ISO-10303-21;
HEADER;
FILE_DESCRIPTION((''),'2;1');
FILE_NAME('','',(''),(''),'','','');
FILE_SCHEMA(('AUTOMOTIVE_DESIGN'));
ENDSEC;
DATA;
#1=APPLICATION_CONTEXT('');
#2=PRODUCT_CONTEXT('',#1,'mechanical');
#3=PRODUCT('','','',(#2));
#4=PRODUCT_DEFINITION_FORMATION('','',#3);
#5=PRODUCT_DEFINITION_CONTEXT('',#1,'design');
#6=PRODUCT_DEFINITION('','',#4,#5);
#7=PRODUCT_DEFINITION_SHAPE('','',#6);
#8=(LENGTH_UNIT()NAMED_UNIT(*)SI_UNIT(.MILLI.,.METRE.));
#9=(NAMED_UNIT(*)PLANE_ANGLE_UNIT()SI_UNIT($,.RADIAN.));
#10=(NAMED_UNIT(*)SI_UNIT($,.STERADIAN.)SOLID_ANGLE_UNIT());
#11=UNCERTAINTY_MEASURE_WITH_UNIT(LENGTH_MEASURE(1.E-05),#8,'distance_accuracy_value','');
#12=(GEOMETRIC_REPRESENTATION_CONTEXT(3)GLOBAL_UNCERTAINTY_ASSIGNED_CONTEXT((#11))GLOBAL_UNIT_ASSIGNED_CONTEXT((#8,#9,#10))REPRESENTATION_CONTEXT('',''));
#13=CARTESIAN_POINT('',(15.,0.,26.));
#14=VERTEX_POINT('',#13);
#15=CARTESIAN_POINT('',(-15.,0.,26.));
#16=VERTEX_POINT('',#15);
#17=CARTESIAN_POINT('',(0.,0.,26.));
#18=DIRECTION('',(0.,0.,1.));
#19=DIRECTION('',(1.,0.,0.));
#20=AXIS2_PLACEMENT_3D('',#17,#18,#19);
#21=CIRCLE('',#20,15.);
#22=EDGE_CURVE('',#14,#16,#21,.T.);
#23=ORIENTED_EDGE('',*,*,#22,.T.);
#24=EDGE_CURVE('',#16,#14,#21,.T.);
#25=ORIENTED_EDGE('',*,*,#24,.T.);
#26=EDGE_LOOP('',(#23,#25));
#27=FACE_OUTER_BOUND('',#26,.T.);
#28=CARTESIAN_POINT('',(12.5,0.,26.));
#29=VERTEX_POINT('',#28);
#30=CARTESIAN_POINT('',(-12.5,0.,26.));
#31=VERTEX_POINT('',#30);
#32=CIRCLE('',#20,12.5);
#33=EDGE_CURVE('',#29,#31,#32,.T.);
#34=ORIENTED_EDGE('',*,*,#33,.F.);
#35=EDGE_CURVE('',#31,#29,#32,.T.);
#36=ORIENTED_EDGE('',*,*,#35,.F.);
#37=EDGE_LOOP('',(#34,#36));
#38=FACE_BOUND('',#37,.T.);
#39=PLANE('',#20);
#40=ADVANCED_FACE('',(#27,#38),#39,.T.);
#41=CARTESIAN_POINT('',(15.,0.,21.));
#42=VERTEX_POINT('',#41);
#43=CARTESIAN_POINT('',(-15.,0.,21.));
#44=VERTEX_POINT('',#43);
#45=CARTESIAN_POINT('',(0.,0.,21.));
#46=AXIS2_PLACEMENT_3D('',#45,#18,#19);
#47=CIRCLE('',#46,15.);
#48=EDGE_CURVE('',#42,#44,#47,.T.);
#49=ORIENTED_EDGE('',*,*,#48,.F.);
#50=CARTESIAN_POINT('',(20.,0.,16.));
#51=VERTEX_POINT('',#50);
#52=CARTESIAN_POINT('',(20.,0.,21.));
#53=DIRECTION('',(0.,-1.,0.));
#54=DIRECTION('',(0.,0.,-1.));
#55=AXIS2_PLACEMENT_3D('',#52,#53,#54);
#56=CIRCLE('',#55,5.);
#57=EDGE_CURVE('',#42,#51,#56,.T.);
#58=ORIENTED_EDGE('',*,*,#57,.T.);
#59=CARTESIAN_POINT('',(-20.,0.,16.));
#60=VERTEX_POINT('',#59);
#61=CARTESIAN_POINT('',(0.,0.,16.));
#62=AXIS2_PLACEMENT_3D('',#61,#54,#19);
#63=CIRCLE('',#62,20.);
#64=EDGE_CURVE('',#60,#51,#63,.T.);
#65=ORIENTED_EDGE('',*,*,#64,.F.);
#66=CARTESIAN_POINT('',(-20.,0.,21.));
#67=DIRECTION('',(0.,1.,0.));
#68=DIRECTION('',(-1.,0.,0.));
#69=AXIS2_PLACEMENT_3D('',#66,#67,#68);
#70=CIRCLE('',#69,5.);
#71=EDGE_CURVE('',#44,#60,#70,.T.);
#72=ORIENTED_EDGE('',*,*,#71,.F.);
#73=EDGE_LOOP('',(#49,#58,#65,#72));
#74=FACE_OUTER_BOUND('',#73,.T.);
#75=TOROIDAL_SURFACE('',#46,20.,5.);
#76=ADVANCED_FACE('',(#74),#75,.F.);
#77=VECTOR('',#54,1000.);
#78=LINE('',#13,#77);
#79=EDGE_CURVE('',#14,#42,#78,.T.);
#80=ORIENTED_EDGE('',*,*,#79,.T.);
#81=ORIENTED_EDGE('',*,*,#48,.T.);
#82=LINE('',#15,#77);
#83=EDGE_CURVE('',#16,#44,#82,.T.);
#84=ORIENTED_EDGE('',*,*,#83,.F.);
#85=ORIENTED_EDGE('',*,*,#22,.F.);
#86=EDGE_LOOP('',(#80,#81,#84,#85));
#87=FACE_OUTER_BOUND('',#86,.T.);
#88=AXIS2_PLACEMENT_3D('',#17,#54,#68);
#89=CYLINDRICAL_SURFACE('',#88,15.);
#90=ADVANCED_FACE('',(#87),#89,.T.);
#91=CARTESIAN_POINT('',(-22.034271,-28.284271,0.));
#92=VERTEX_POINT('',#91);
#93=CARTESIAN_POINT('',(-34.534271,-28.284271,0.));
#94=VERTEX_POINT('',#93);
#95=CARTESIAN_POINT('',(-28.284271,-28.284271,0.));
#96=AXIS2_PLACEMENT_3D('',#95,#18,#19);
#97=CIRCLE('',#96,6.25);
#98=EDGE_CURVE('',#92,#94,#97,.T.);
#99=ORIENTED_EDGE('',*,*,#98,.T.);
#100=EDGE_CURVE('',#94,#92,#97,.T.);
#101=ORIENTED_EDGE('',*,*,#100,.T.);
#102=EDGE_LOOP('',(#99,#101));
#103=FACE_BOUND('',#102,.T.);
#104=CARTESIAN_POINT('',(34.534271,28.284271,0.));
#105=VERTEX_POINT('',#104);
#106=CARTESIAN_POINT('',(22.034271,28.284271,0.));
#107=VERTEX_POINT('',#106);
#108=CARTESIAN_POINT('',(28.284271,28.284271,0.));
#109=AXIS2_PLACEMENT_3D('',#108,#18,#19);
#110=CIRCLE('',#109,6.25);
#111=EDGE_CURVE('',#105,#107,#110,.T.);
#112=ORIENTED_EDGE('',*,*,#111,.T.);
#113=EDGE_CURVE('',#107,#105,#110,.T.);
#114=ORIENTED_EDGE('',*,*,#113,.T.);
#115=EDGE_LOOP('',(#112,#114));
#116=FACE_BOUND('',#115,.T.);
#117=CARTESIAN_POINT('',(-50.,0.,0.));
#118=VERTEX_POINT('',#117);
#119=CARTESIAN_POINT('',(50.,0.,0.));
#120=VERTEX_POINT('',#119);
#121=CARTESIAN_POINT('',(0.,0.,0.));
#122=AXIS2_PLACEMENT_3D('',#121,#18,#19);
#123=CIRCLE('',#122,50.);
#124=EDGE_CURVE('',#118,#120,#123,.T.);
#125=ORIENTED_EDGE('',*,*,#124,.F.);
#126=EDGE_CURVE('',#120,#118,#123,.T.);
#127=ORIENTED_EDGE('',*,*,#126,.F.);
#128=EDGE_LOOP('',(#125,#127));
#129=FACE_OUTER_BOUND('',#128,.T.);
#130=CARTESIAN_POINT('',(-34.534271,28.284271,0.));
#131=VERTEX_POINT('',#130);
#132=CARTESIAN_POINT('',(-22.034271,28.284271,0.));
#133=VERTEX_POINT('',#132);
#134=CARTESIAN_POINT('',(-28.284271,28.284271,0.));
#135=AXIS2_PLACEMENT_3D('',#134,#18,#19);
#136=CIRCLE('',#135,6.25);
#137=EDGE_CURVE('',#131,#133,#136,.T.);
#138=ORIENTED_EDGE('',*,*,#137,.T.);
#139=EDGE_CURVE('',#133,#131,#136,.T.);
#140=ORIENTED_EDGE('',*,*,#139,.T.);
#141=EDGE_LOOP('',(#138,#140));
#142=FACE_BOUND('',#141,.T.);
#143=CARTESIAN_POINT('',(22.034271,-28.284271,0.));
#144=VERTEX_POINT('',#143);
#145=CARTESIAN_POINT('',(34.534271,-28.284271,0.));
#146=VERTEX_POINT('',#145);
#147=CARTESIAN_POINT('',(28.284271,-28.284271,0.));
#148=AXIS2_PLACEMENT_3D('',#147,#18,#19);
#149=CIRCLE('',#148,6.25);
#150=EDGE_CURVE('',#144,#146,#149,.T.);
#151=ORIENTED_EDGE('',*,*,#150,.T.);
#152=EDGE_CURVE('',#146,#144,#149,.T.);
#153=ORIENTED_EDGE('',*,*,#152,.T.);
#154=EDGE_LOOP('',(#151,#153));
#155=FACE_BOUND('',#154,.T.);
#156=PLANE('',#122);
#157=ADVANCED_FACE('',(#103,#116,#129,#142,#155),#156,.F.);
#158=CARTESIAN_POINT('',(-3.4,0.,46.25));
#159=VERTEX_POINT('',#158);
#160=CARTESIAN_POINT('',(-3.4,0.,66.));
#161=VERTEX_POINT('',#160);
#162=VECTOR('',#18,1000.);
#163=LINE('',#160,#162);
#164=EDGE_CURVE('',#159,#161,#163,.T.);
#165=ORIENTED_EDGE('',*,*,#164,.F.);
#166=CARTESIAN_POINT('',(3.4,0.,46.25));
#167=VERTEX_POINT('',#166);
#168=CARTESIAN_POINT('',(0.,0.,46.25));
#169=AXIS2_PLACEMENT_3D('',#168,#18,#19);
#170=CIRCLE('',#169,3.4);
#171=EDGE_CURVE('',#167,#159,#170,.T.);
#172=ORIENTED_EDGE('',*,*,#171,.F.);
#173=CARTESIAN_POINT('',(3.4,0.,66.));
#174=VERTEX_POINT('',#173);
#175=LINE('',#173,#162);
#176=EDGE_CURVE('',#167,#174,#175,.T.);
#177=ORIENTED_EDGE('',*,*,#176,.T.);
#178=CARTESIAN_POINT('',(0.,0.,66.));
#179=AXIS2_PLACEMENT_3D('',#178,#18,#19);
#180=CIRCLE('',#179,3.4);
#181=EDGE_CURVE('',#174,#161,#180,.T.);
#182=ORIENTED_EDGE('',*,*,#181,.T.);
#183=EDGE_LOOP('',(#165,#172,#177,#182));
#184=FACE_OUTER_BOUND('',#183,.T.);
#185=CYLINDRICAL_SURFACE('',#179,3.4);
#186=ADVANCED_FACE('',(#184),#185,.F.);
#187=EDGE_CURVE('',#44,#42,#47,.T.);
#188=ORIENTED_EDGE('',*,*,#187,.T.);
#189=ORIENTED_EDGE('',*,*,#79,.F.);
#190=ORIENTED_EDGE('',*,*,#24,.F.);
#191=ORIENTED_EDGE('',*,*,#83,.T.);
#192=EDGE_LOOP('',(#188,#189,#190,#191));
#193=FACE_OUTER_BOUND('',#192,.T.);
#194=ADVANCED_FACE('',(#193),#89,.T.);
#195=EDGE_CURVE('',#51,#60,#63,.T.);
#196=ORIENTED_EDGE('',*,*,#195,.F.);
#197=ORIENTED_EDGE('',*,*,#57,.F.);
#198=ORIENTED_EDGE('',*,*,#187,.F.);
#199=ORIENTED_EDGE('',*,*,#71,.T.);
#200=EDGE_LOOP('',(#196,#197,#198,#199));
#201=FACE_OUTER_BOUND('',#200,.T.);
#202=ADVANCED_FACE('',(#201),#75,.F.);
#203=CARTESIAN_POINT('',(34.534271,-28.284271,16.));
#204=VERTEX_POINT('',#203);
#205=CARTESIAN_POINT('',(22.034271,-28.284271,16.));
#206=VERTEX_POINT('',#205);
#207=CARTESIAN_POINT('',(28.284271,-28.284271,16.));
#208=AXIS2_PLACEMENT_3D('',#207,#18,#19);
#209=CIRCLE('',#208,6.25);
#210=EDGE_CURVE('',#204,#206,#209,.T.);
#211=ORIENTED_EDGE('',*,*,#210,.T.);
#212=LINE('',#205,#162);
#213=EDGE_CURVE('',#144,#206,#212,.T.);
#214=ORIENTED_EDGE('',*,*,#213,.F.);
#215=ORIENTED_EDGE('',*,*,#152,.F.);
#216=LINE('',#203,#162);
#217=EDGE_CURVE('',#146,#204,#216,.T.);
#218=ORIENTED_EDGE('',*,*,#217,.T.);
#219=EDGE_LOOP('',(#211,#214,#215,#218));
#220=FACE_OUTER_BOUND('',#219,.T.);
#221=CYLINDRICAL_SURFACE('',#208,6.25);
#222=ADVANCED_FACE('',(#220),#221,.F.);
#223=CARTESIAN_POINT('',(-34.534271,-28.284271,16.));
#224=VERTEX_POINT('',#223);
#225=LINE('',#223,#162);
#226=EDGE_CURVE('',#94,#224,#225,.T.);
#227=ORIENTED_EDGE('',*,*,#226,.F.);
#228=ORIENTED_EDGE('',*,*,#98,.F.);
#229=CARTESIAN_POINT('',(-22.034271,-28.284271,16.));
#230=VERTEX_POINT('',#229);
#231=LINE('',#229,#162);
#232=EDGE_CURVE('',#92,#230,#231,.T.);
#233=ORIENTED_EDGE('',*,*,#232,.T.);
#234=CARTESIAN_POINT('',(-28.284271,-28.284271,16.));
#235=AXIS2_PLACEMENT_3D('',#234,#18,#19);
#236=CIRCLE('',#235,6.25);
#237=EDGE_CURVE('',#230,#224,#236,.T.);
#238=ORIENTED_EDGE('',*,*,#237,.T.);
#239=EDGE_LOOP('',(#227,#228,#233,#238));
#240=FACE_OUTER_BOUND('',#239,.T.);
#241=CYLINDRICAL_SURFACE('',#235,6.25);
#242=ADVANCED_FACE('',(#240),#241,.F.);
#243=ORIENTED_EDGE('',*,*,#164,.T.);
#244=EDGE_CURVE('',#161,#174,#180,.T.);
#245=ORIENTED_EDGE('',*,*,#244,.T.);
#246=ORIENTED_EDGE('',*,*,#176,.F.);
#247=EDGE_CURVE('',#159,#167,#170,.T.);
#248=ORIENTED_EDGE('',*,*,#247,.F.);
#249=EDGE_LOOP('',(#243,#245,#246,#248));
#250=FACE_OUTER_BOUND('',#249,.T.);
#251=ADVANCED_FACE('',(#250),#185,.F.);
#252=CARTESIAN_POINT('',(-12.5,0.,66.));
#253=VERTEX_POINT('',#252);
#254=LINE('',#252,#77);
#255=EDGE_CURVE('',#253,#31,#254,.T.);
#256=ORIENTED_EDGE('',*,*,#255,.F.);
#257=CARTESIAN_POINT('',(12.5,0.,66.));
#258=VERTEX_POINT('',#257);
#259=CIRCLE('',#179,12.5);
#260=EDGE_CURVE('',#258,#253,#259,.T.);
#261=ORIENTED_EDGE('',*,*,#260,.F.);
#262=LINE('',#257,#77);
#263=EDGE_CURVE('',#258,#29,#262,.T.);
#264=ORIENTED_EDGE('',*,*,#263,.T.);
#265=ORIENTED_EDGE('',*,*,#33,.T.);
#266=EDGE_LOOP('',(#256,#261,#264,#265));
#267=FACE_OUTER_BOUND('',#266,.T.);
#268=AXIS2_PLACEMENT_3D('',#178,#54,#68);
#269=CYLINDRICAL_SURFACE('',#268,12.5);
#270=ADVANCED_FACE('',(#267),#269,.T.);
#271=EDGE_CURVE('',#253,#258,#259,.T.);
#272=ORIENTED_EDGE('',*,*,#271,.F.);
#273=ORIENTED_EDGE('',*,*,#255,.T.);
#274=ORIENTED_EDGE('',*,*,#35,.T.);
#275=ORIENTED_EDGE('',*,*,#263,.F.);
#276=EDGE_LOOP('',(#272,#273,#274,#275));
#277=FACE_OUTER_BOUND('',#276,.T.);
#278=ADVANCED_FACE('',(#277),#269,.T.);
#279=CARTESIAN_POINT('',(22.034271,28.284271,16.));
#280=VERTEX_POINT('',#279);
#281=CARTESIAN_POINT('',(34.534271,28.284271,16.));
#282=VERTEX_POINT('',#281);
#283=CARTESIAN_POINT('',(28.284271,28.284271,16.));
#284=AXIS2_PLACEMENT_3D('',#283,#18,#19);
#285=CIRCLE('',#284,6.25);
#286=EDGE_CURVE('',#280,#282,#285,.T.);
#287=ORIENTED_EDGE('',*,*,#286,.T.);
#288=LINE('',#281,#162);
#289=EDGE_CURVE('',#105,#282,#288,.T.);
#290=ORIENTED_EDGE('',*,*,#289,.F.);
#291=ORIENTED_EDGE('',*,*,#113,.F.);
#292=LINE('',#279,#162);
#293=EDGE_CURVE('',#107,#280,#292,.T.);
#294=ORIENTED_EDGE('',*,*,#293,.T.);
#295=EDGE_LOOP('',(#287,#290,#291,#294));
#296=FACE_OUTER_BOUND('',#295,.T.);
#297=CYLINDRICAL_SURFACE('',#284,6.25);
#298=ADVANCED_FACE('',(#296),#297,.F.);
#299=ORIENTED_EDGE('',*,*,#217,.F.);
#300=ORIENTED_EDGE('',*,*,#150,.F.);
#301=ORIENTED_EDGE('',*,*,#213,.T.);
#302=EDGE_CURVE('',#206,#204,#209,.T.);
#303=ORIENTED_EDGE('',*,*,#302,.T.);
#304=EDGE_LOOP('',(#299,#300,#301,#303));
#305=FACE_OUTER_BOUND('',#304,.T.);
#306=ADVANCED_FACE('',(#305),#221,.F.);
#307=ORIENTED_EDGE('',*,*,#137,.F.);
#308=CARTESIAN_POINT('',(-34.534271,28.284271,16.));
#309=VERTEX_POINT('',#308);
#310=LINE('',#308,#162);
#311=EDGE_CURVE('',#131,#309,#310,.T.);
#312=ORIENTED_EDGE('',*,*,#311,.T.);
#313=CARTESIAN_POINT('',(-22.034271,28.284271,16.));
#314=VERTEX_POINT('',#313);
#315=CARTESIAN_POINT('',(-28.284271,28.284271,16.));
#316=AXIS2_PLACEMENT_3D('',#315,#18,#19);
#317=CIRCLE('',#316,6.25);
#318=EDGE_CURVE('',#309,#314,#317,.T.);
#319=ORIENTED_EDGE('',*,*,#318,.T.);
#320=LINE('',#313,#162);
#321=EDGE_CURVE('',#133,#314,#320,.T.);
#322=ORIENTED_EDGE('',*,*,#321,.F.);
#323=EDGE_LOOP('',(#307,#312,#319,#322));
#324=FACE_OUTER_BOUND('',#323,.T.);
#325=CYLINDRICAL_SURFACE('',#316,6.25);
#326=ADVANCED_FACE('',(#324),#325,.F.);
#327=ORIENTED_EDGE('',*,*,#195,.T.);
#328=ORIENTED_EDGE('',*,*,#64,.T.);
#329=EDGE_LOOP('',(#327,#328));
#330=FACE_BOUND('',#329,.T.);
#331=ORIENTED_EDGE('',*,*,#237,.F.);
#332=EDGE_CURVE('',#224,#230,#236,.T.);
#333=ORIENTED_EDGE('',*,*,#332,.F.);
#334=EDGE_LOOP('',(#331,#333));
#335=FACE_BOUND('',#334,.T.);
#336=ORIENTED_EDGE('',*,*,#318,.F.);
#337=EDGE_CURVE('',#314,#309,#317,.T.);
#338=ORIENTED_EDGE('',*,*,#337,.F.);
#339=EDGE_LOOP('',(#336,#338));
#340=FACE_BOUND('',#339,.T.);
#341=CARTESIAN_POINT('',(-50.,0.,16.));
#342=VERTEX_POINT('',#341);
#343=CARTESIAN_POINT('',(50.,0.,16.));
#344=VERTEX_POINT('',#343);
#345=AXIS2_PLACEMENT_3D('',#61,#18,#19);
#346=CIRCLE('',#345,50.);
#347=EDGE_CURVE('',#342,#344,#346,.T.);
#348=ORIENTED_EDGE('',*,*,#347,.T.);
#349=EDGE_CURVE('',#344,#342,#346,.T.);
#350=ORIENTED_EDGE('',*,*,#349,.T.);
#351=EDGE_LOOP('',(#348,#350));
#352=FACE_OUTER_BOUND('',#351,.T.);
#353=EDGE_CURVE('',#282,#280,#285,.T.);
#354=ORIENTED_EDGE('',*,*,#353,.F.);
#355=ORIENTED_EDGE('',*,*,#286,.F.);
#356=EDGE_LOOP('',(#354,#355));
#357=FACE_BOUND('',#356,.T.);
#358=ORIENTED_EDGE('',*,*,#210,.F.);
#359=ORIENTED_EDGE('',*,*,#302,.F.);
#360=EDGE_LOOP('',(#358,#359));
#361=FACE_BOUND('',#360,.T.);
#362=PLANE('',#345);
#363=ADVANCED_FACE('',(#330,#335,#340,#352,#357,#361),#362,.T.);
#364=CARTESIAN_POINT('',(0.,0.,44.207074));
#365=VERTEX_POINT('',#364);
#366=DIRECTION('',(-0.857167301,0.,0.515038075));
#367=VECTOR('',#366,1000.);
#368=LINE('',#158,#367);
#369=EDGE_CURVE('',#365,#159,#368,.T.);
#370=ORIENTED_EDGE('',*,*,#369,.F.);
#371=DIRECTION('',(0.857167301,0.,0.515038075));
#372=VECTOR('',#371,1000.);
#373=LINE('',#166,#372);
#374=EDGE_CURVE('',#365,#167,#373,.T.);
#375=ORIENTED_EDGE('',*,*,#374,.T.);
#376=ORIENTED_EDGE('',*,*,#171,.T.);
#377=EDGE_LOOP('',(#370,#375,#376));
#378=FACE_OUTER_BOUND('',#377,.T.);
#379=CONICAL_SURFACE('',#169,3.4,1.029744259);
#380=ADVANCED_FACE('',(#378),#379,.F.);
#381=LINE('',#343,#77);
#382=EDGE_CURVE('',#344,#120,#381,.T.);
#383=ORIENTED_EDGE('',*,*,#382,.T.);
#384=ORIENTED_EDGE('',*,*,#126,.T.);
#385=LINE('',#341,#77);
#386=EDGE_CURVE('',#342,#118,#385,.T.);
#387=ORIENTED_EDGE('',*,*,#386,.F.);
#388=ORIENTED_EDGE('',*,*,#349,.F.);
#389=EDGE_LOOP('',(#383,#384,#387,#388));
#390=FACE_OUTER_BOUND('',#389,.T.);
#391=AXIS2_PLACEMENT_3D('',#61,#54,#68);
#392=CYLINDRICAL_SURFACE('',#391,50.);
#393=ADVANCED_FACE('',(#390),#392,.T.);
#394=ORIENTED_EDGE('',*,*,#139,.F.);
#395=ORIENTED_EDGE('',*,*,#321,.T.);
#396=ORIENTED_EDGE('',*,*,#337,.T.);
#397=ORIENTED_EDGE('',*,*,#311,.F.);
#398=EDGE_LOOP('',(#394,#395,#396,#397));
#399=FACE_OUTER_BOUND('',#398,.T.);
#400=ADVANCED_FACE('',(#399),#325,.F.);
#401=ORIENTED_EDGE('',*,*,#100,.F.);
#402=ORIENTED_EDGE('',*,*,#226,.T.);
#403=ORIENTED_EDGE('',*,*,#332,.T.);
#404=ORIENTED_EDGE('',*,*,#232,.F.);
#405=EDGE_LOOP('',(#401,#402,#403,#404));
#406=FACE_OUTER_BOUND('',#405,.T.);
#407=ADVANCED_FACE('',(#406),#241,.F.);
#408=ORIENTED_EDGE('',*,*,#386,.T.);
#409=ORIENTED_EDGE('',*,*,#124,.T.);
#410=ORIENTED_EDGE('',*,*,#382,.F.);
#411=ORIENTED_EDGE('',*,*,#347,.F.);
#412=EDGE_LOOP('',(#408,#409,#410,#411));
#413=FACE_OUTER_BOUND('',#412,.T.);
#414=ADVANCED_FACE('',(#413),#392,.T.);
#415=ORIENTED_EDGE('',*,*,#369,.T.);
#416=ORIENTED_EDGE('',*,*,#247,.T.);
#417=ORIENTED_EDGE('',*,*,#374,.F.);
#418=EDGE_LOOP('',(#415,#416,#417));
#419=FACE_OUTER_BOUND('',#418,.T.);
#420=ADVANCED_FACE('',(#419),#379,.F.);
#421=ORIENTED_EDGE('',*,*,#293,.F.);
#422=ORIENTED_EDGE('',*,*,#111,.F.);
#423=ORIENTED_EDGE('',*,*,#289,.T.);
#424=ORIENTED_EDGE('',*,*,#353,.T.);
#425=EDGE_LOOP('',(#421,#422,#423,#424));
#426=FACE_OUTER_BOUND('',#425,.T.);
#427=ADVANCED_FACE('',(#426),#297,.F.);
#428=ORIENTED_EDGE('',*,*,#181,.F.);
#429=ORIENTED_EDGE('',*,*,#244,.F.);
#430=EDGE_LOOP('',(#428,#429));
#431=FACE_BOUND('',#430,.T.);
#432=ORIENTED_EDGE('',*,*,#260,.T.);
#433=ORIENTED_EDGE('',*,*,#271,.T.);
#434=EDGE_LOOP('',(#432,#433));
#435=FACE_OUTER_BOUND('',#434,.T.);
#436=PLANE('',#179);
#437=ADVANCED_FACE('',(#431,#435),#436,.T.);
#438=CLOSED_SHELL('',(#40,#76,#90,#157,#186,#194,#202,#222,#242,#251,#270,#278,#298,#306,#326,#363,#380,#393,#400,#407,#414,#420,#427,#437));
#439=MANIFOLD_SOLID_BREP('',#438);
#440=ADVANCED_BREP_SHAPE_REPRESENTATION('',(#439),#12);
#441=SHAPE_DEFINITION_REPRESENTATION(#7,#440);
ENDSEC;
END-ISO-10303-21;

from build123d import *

# Parameters (mm, degrees)
SKETCH_1_R                = 50
EXTRUDE_1_DEPTH           = 16
SKETCH_2_R                = 15
EXTRUDE_2_DEPTH           = 10
SKETCH_3_R                = 12.5
EXTRUDE_3_DEPTH           = 40
HOLE_WIZARD_12_5_12_5_1_D = 12.5
PATTERN_CIRCULAR_1_COUNT  = 4
HOLE_WIZARD_M8_1_D        = 6.8
HOLE_WIZARD_M8_1_DEPTH    = 19.75
HOLE_WIZARD_M8_1_TIP      = 2.042926105
FILLET_1_R                = 5


with BuildPart() as part:
    # 草图1 → 凸台-拉伸1 (new body)
    with BuildSketch(Plane.XY):
        Circle(SKETCH_1_R)
    extrude(amount=EXTRUDE_1_DEPTH)

    # 草图2 → 凸台-拉伸2 (add)
    with BuildSketch(Plane.XY.offset(16)):
        Circle(SKETCH_2_R)
    extrude(amount=EXTRUDE_2_DEPTH)

    # 草图3 → 凸台-拉伸3 (add)
    with BuildSketch(Plane.XY.offset(26)):
        Circle(SKETCH_3_R)
    extrude(amount=EXTRUDE_3_DEPTH)

    # Ø12.5 (12.5) 直径孔1 (through all)
    with Locations(Plane.XY.offset(16)):
        with Locations((-28.284271247, 28.284271247)):
            hole_wizard_12_5_12_5_1 = Hole(HOLE_WIZARD_12_5_12_5_1_D / 2)

    # 阵列(圆周)1: Ø12.5 (12.5) 直径孔1 ×4 about axis
    pattern_circular_1_axis = Axis((0, 0, 0), (0, 0, 1))
    for i in range(1, PATTERN_CIRCULAR_1_COUNT):
        add(hole_wizard_12_5_12_5_1.rotate(pattern_circular_1_axis, i * 360 / PATTERN_CIRCULAR_1_COUNT), mode=Mode.SUBTRACT)

    # M8 螺纹孔1
    with Locations(Plane.XY.offset(66)):
        with Locations((0, 0)):
            Hole(HOLE_WIZARD_M8_1_D / 2, depth=HOLE_WIZARD_M8_1_DEPTH)
            with Locations((0, 0, -(HOLE_WIZARD_M8_1_DEPTH + HOLE_WIZARD_M8_1_TIP / 2))):  # 118° drill point
                Cone(0, HOLE_WIZARD_M8_1_D / 2, HOLE_WIZARD_M8_1_TIP, mode=Mode.SUBTRACT)

    # 圆角1
    fillet_1_edges = [part.edges().sort_by_distance(p)[0] for p in [
        (-15, 0, 16),
    ]]
    fillet(fillet_1_edges, radius=FILLET_1_R)


solid = part.part
